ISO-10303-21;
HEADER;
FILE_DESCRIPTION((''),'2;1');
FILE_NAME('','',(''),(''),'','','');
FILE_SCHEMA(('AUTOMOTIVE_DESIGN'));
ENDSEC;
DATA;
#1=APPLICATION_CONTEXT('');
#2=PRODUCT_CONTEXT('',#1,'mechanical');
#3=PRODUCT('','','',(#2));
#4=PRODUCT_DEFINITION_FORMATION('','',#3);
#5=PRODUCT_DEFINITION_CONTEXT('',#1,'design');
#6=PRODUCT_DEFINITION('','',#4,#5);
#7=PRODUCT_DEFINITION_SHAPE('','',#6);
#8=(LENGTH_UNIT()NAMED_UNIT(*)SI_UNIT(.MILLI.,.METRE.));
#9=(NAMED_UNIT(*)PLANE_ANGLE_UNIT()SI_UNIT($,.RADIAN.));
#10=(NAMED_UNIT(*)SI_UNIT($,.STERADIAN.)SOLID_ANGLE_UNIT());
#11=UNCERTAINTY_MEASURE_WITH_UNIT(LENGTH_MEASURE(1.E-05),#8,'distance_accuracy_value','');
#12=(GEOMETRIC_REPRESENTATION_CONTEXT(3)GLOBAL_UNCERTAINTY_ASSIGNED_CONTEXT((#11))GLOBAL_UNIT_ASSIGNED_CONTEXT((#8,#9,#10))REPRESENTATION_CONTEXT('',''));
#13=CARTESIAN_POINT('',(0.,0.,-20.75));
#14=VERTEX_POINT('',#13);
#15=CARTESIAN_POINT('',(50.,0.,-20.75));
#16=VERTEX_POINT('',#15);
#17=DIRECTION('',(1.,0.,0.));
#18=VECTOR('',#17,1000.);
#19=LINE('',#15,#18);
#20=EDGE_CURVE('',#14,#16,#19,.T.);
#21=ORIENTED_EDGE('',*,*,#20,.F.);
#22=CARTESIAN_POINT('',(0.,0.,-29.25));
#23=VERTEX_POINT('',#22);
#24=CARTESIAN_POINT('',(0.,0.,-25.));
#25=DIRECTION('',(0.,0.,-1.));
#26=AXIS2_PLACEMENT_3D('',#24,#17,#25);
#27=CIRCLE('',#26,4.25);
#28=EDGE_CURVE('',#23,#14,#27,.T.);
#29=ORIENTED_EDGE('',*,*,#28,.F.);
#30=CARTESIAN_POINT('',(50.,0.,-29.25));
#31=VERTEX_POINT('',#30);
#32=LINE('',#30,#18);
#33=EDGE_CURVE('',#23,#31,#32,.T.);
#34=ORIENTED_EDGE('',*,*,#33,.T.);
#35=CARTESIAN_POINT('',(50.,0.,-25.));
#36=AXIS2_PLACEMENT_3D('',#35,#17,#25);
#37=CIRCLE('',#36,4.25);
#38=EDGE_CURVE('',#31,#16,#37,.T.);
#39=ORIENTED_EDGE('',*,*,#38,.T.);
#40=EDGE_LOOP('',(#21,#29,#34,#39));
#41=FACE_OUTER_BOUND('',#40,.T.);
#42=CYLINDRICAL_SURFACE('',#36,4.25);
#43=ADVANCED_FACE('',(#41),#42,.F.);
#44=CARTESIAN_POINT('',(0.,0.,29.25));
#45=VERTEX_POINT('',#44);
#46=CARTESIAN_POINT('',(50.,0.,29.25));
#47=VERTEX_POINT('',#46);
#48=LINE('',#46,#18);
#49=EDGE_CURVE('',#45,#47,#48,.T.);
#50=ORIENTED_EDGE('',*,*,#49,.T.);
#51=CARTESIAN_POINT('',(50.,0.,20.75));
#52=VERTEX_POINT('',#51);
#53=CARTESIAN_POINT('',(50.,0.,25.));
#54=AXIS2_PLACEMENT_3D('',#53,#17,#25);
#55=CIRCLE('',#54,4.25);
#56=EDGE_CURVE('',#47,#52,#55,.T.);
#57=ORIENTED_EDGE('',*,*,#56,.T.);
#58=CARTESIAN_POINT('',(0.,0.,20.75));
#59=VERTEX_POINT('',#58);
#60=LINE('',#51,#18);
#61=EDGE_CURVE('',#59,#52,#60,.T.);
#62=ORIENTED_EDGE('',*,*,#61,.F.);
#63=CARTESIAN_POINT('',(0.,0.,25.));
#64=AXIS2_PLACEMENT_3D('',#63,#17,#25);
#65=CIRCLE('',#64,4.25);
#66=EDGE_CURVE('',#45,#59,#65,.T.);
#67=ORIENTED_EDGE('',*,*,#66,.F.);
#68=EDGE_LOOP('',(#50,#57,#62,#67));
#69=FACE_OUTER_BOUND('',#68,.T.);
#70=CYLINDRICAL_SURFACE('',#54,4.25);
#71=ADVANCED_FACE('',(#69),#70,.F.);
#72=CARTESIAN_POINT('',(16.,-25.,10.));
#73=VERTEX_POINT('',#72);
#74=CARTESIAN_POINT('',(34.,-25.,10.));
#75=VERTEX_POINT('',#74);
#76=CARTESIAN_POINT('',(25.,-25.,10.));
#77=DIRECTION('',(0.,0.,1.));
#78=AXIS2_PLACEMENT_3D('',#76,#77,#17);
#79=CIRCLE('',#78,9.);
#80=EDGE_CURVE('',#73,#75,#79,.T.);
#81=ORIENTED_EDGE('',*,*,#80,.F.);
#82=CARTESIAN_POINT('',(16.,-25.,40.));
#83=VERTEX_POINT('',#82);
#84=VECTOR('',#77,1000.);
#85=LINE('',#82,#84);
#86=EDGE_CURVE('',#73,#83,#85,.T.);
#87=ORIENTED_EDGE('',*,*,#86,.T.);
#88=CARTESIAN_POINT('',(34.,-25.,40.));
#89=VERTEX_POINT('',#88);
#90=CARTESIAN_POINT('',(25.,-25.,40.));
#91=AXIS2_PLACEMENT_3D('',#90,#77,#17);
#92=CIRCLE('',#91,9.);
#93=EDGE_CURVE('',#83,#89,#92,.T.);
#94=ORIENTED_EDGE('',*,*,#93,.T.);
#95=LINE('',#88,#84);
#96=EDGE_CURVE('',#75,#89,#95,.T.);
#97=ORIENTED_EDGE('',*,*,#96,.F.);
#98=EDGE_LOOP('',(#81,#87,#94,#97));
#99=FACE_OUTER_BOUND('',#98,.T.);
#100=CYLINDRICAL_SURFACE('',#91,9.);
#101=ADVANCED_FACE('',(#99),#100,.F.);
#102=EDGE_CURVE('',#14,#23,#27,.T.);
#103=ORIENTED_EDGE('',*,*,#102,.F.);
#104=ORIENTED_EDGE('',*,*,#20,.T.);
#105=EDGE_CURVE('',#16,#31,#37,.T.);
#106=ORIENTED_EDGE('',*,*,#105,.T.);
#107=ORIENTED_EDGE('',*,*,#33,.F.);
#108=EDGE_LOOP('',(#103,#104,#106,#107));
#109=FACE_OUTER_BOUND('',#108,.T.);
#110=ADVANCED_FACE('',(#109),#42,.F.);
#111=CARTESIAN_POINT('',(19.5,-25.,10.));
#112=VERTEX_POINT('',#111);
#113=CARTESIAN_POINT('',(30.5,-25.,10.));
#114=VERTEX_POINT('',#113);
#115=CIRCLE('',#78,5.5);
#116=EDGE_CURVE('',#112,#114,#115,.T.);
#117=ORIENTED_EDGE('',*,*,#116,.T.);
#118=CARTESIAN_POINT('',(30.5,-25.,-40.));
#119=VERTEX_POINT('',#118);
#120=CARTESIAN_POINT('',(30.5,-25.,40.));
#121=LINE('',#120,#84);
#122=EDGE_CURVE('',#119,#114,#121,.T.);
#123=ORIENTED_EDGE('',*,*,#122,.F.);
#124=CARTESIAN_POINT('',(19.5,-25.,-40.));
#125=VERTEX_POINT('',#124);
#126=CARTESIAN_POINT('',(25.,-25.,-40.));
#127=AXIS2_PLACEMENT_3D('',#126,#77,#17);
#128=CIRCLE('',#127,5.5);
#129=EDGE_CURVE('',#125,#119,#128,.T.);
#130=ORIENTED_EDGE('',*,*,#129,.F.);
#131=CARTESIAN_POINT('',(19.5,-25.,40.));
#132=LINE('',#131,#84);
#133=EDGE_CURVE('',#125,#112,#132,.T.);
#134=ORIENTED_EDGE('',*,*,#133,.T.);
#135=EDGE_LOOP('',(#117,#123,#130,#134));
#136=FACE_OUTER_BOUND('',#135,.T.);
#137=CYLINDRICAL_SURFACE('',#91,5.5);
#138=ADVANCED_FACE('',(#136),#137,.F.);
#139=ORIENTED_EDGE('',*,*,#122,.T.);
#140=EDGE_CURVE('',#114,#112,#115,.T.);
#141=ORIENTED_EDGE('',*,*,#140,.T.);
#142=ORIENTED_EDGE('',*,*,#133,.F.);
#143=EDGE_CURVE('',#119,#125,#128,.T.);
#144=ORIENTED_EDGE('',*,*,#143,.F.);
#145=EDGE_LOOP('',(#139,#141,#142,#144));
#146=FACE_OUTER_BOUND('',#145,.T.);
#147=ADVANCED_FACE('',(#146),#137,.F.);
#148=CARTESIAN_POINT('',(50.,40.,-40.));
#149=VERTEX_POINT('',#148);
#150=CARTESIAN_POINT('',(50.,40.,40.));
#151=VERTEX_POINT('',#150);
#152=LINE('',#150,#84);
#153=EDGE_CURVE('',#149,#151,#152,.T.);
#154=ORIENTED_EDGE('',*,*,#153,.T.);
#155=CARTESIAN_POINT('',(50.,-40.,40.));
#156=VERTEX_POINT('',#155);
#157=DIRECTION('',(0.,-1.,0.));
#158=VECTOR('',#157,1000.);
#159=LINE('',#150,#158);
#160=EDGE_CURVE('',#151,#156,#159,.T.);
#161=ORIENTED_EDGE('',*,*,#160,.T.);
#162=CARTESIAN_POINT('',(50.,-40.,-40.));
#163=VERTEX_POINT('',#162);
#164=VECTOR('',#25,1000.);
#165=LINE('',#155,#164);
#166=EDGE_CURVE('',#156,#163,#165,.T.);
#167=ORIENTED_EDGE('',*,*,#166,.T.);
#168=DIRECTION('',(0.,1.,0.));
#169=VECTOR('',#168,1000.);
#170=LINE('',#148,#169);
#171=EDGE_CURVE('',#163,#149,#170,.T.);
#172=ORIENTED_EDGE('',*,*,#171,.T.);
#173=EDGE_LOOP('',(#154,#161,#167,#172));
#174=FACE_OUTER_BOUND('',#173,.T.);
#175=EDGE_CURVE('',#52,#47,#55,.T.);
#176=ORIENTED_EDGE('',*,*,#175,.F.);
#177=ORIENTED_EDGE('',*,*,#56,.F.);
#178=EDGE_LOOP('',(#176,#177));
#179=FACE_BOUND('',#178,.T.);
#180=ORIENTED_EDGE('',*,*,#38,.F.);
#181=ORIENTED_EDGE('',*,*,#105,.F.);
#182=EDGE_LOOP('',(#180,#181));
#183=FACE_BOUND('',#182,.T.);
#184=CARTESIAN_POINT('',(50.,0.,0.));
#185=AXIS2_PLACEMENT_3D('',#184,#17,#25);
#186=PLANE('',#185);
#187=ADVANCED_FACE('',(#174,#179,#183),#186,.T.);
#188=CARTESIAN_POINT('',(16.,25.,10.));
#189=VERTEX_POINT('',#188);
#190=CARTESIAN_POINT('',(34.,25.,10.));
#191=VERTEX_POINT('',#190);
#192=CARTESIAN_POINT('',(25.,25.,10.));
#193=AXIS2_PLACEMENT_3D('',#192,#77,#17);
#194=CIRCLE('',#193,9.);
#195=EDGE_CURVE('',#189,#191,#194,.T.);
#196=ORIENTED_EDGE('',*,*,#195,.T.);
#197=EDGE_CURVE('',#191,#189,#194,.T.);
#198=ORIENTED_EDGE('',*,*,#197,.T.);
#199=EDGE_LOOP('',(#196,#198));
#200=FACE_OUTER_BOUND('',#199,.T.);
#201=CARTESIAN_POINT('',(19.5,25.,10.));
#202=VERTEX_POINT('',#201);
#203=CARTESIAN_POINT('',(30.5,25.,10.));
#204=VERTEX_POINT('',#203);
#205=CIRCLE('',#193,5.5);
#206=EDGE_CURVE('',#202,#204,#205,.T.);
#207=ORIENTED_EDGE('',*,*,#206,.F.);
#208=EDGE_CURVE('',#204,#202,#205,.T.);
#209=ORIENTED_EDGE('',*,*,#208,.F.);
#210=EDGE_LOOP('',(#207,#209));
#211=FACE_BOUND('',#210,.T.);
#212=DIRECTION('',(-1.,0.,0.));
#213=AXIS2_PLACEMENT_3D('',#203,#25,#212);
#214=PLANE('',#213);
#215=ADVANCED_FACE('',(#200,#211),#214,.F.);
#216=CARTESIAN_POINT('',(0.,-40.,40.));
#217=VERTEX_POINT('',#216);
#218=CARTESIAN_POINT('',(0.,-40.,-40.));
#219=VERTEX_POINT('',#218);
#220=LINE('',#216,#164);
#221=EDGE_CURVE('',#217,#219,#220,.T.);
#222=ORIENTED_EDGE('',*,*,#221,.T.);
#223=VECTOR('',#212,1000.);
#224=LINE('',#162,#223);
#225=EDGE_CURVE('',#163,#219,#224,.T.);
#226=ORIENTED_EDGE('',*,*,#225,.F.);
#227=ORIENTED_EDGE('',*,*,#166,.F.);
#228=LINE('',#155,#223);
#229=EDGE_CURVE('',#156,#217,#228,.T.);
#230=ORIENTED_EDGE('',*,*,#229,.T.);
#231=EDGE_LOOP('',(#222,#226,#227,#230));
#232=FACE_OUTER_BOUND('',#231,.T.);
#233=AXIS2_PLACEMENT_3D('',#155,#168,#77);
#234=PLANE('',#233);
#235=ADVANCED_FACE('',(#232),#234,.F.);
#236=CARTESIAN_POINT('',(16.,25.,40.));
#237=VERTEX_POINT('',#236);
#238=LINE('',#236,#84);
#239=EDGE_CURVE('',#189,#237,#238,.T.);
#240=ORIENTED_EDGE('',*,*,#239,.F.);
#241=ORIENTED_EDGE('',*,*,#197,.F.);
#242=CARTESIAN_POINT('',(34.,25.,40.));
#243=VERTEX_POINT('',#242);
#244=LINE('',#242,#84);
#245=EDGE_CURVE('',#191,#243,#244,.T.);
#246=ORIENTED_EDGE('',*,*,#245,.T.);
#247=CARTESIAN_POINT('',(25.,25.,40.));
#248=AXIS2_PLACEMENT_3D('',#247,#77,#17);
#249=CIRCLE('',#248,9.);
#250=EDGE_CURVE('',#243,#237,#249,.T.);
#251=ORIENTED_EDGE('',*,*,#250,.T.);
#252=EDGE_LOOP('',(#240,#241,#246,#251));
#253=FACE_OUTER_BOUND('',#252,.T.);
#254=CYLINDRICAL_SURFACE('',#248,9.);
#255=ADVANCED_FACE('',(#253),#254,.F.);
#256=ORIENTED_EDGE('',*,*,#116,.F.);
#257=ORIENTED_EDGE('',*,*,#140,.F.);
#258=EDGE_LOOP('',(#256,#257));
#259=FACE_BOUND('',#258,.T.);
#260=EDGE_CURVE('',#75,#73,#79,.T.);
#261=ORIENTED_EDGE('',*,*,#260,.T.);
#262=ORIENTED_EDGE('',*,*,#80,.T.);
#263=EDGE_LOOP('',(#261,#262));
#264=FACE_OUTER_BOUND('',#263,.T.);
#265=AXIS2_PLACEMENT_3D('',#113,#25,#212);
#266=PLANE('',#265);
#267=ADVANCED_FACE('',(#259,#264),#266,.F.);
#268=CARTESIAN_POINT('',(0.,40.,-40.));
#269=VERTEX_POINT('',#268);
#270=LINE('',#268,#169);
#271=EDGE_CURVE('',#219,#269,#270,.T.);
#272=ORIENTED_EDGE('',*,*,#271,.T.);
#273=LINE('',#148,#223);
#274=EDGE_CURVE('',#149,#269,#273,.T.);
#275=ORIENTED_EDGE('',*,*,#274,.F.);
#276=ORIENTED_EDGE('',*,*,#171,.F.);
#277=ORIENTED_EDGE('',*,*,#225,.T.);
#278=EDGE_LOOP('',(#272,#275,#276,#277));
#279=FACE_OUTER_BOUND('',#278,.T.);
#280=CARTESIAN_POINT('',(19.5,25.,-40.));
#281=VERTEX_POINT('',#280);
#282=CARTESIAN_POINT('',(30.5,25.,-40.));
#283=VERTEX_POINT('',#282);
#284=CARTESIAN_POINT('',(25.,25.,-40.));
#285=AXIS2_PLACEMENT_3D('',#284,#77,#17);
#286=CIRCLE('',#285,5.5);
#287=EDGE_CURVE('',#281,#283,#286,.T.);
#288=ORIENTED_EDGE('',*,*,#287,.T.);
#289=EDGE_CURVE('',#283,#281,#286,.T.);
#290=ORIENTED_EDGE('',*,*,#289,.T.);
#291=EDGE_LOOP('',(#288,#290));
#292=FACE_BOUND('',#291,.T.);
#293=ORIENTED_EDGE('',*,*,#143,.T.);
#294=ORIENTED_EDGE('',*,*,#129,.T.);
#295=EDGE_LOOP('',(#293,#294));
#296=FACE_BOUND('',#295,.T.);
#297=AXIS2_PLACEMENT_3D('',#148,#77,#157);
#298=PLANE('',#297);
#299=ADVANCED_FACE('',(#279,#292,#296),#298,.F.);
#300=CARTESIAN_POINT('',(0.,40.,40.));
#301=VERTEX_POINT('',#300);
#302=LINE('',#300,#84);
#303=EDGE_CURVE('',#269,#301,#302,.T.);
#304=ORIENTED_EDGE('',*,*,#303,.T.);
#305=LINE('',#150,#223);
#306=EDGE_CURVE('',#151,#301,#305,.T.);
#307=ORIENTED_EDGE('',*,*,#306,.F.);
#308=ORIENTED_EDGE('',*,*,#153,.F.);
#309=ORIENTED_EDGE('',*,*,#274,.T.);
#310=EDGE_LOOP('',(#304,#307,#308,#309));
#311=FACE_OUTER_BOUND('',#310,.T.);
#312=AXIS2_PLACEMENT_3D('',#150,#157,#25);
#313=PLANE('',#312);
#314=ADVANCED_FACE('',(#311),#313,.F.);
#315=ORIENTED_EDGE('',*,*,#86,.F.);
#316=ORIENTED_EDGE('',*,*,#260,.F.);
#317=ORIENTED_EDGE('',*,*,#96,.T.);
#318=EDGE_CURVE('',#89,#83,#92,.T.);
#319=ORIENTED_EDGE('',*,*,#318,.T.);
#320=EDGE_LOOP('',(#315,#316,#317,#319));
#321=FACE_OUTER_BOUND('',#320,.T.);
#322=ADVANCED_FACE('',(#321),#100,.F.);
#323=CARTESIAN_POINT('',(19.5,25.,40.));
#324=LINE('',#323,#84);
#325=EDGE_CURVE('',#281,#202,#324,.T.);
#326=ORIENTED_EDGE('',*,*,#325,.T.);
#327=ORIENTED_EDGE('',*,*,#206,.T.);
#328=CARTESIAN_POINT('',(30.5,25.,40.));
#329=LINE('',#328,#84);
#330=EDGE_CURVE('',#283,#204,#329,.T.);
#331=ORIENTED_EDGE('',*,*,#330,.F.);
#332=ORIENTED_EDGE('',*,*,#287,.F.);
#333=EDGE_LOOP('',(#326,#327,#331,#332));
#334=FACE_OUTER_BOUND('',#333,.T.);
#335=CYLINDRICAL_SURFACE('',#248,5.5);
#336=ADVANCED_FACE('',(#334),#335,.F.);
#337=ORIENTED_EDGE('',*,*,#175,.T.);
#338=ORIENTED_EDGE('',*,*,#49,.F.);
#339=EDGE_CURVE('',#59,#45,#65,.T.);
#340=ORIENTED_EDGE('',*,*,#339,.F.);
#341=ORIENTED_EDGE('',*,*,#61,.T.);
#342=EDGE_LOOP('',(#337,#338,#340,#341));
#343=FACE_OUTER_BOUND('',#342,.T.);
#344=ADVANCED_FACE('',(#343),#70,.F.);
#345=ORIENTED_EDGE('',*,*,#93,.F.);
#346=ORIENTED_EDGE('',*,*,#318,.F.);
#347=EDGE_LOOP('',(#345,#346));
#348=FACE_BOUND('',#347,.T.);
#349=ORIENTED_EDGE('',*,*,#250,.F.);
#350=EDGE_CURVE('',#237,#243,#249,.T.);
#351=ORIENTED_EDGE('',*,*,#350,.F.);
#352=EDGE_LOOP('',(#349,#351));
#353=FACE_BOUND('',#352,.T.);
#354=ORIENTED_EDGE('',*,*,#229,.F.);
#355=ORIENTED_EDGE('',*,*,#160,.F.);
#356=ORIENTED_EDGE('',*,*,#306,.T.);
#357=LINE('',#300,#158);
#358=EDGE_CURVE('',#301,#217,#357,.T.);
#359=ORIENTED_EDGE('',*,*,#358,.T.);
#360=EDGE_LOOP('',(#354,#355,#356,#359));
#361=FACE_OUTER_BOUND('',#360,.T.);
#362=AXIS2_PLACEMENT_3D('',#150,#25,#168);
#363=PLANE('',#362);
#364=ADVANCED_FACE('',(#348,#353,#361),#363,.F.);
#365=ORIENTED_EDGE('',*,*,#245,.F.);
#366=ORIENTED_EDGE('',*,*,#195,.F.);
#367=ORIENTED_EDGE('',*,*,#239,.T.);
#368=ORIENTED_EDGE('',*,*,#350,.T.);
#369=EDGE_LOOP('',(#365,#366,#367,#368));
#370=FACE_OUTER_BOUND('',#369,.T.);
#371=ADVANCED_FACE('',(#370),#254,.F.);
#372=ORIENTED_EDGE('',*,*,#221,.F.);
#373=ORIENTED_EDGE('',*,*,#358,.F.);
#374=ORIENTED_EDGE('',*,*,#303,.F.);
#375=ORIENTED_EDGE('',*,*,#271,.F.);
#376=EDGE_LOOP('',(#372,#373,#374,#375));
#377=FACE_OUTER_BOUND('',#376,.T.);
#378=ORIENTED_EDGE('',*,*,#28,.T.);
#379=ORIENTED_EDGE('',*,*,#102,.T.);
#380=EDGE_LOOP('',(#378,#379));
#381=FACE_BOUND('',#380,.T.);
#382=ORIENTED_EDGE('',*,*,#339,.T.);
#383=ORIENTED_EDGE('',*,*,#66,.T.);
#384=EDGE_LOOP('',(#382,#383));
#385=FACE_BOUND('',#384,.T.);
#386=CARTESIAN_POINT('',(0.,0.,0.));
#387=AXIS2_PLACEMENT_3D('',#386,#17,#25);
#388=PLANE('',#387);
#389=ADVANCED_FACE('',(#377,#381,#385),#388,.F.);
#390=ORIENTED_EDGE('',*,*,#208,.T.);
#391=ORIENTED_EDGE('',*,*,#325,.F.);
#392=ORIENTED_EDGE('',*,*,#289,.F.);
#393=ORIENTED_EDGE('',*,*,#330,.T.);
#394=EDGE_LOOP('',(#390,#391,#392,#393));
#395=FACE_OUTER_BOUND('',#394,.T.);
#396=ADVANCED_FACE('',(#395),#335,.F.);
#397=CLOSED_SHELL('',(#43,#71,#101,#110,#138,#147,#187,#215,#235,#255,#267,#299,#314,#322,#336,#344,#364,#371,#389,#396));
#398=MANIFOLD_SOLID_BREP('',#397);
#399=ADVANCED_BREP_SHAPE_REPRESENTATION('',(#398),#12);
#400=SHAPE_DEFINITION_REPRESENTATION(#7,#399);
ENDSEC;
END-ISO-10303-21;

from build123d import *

# Parameters (mm, degrees)
SKETCH_1_W                = 80
SKETCH_1_H                = 80
EXTRUDE_1_DEPTH           = 50
HOLE_WIZARD_1_D           = 11
HOLE_WIZARD_1_CBORE_D     = 18
HOLE_WIZARD_1_CBORE_DEPTH = 30
HOLE_WIZARD_M10_1_D       = 8.5


with BuildPart() as part:
    # 草图1 → 凸台-拉伸1 (new body)
    with BuildSketch(Plane(origin=(0, 0, 0), x_dir=(0, 0, -1), z_dir=(1, 0, 0))):
        Rectangle(SKETCH_1_W, SKETCH_1_H)
    extrude(amount=EXTRUDE_1_DEPTH)

    # 打孔尺寸(%根据)内六角圆柱头螺钉的类型1 (through all)
    with Locations(Plane.XY.offset(40)):
        with Locations((25, 25), (25, -25)):
            CounterBoreHole(HOLE_WIZARD_1_D / 2, HOLE_WIZARD_1_CBORE_D / 2, HOLE_WIZARD_1_CBORE_DEPTH)

    # M10 螺纹孔1 (through all)
    with Locations(Plane(origin=(50, 0, 0), x_dir=(0, 0, -1), z_dir=(1, 0, 0))):
        with Locations((25, 0), (-25, 0)):
            Hole(HOLE_WIZARD_M10_1_D / 2)


solid = part.part
